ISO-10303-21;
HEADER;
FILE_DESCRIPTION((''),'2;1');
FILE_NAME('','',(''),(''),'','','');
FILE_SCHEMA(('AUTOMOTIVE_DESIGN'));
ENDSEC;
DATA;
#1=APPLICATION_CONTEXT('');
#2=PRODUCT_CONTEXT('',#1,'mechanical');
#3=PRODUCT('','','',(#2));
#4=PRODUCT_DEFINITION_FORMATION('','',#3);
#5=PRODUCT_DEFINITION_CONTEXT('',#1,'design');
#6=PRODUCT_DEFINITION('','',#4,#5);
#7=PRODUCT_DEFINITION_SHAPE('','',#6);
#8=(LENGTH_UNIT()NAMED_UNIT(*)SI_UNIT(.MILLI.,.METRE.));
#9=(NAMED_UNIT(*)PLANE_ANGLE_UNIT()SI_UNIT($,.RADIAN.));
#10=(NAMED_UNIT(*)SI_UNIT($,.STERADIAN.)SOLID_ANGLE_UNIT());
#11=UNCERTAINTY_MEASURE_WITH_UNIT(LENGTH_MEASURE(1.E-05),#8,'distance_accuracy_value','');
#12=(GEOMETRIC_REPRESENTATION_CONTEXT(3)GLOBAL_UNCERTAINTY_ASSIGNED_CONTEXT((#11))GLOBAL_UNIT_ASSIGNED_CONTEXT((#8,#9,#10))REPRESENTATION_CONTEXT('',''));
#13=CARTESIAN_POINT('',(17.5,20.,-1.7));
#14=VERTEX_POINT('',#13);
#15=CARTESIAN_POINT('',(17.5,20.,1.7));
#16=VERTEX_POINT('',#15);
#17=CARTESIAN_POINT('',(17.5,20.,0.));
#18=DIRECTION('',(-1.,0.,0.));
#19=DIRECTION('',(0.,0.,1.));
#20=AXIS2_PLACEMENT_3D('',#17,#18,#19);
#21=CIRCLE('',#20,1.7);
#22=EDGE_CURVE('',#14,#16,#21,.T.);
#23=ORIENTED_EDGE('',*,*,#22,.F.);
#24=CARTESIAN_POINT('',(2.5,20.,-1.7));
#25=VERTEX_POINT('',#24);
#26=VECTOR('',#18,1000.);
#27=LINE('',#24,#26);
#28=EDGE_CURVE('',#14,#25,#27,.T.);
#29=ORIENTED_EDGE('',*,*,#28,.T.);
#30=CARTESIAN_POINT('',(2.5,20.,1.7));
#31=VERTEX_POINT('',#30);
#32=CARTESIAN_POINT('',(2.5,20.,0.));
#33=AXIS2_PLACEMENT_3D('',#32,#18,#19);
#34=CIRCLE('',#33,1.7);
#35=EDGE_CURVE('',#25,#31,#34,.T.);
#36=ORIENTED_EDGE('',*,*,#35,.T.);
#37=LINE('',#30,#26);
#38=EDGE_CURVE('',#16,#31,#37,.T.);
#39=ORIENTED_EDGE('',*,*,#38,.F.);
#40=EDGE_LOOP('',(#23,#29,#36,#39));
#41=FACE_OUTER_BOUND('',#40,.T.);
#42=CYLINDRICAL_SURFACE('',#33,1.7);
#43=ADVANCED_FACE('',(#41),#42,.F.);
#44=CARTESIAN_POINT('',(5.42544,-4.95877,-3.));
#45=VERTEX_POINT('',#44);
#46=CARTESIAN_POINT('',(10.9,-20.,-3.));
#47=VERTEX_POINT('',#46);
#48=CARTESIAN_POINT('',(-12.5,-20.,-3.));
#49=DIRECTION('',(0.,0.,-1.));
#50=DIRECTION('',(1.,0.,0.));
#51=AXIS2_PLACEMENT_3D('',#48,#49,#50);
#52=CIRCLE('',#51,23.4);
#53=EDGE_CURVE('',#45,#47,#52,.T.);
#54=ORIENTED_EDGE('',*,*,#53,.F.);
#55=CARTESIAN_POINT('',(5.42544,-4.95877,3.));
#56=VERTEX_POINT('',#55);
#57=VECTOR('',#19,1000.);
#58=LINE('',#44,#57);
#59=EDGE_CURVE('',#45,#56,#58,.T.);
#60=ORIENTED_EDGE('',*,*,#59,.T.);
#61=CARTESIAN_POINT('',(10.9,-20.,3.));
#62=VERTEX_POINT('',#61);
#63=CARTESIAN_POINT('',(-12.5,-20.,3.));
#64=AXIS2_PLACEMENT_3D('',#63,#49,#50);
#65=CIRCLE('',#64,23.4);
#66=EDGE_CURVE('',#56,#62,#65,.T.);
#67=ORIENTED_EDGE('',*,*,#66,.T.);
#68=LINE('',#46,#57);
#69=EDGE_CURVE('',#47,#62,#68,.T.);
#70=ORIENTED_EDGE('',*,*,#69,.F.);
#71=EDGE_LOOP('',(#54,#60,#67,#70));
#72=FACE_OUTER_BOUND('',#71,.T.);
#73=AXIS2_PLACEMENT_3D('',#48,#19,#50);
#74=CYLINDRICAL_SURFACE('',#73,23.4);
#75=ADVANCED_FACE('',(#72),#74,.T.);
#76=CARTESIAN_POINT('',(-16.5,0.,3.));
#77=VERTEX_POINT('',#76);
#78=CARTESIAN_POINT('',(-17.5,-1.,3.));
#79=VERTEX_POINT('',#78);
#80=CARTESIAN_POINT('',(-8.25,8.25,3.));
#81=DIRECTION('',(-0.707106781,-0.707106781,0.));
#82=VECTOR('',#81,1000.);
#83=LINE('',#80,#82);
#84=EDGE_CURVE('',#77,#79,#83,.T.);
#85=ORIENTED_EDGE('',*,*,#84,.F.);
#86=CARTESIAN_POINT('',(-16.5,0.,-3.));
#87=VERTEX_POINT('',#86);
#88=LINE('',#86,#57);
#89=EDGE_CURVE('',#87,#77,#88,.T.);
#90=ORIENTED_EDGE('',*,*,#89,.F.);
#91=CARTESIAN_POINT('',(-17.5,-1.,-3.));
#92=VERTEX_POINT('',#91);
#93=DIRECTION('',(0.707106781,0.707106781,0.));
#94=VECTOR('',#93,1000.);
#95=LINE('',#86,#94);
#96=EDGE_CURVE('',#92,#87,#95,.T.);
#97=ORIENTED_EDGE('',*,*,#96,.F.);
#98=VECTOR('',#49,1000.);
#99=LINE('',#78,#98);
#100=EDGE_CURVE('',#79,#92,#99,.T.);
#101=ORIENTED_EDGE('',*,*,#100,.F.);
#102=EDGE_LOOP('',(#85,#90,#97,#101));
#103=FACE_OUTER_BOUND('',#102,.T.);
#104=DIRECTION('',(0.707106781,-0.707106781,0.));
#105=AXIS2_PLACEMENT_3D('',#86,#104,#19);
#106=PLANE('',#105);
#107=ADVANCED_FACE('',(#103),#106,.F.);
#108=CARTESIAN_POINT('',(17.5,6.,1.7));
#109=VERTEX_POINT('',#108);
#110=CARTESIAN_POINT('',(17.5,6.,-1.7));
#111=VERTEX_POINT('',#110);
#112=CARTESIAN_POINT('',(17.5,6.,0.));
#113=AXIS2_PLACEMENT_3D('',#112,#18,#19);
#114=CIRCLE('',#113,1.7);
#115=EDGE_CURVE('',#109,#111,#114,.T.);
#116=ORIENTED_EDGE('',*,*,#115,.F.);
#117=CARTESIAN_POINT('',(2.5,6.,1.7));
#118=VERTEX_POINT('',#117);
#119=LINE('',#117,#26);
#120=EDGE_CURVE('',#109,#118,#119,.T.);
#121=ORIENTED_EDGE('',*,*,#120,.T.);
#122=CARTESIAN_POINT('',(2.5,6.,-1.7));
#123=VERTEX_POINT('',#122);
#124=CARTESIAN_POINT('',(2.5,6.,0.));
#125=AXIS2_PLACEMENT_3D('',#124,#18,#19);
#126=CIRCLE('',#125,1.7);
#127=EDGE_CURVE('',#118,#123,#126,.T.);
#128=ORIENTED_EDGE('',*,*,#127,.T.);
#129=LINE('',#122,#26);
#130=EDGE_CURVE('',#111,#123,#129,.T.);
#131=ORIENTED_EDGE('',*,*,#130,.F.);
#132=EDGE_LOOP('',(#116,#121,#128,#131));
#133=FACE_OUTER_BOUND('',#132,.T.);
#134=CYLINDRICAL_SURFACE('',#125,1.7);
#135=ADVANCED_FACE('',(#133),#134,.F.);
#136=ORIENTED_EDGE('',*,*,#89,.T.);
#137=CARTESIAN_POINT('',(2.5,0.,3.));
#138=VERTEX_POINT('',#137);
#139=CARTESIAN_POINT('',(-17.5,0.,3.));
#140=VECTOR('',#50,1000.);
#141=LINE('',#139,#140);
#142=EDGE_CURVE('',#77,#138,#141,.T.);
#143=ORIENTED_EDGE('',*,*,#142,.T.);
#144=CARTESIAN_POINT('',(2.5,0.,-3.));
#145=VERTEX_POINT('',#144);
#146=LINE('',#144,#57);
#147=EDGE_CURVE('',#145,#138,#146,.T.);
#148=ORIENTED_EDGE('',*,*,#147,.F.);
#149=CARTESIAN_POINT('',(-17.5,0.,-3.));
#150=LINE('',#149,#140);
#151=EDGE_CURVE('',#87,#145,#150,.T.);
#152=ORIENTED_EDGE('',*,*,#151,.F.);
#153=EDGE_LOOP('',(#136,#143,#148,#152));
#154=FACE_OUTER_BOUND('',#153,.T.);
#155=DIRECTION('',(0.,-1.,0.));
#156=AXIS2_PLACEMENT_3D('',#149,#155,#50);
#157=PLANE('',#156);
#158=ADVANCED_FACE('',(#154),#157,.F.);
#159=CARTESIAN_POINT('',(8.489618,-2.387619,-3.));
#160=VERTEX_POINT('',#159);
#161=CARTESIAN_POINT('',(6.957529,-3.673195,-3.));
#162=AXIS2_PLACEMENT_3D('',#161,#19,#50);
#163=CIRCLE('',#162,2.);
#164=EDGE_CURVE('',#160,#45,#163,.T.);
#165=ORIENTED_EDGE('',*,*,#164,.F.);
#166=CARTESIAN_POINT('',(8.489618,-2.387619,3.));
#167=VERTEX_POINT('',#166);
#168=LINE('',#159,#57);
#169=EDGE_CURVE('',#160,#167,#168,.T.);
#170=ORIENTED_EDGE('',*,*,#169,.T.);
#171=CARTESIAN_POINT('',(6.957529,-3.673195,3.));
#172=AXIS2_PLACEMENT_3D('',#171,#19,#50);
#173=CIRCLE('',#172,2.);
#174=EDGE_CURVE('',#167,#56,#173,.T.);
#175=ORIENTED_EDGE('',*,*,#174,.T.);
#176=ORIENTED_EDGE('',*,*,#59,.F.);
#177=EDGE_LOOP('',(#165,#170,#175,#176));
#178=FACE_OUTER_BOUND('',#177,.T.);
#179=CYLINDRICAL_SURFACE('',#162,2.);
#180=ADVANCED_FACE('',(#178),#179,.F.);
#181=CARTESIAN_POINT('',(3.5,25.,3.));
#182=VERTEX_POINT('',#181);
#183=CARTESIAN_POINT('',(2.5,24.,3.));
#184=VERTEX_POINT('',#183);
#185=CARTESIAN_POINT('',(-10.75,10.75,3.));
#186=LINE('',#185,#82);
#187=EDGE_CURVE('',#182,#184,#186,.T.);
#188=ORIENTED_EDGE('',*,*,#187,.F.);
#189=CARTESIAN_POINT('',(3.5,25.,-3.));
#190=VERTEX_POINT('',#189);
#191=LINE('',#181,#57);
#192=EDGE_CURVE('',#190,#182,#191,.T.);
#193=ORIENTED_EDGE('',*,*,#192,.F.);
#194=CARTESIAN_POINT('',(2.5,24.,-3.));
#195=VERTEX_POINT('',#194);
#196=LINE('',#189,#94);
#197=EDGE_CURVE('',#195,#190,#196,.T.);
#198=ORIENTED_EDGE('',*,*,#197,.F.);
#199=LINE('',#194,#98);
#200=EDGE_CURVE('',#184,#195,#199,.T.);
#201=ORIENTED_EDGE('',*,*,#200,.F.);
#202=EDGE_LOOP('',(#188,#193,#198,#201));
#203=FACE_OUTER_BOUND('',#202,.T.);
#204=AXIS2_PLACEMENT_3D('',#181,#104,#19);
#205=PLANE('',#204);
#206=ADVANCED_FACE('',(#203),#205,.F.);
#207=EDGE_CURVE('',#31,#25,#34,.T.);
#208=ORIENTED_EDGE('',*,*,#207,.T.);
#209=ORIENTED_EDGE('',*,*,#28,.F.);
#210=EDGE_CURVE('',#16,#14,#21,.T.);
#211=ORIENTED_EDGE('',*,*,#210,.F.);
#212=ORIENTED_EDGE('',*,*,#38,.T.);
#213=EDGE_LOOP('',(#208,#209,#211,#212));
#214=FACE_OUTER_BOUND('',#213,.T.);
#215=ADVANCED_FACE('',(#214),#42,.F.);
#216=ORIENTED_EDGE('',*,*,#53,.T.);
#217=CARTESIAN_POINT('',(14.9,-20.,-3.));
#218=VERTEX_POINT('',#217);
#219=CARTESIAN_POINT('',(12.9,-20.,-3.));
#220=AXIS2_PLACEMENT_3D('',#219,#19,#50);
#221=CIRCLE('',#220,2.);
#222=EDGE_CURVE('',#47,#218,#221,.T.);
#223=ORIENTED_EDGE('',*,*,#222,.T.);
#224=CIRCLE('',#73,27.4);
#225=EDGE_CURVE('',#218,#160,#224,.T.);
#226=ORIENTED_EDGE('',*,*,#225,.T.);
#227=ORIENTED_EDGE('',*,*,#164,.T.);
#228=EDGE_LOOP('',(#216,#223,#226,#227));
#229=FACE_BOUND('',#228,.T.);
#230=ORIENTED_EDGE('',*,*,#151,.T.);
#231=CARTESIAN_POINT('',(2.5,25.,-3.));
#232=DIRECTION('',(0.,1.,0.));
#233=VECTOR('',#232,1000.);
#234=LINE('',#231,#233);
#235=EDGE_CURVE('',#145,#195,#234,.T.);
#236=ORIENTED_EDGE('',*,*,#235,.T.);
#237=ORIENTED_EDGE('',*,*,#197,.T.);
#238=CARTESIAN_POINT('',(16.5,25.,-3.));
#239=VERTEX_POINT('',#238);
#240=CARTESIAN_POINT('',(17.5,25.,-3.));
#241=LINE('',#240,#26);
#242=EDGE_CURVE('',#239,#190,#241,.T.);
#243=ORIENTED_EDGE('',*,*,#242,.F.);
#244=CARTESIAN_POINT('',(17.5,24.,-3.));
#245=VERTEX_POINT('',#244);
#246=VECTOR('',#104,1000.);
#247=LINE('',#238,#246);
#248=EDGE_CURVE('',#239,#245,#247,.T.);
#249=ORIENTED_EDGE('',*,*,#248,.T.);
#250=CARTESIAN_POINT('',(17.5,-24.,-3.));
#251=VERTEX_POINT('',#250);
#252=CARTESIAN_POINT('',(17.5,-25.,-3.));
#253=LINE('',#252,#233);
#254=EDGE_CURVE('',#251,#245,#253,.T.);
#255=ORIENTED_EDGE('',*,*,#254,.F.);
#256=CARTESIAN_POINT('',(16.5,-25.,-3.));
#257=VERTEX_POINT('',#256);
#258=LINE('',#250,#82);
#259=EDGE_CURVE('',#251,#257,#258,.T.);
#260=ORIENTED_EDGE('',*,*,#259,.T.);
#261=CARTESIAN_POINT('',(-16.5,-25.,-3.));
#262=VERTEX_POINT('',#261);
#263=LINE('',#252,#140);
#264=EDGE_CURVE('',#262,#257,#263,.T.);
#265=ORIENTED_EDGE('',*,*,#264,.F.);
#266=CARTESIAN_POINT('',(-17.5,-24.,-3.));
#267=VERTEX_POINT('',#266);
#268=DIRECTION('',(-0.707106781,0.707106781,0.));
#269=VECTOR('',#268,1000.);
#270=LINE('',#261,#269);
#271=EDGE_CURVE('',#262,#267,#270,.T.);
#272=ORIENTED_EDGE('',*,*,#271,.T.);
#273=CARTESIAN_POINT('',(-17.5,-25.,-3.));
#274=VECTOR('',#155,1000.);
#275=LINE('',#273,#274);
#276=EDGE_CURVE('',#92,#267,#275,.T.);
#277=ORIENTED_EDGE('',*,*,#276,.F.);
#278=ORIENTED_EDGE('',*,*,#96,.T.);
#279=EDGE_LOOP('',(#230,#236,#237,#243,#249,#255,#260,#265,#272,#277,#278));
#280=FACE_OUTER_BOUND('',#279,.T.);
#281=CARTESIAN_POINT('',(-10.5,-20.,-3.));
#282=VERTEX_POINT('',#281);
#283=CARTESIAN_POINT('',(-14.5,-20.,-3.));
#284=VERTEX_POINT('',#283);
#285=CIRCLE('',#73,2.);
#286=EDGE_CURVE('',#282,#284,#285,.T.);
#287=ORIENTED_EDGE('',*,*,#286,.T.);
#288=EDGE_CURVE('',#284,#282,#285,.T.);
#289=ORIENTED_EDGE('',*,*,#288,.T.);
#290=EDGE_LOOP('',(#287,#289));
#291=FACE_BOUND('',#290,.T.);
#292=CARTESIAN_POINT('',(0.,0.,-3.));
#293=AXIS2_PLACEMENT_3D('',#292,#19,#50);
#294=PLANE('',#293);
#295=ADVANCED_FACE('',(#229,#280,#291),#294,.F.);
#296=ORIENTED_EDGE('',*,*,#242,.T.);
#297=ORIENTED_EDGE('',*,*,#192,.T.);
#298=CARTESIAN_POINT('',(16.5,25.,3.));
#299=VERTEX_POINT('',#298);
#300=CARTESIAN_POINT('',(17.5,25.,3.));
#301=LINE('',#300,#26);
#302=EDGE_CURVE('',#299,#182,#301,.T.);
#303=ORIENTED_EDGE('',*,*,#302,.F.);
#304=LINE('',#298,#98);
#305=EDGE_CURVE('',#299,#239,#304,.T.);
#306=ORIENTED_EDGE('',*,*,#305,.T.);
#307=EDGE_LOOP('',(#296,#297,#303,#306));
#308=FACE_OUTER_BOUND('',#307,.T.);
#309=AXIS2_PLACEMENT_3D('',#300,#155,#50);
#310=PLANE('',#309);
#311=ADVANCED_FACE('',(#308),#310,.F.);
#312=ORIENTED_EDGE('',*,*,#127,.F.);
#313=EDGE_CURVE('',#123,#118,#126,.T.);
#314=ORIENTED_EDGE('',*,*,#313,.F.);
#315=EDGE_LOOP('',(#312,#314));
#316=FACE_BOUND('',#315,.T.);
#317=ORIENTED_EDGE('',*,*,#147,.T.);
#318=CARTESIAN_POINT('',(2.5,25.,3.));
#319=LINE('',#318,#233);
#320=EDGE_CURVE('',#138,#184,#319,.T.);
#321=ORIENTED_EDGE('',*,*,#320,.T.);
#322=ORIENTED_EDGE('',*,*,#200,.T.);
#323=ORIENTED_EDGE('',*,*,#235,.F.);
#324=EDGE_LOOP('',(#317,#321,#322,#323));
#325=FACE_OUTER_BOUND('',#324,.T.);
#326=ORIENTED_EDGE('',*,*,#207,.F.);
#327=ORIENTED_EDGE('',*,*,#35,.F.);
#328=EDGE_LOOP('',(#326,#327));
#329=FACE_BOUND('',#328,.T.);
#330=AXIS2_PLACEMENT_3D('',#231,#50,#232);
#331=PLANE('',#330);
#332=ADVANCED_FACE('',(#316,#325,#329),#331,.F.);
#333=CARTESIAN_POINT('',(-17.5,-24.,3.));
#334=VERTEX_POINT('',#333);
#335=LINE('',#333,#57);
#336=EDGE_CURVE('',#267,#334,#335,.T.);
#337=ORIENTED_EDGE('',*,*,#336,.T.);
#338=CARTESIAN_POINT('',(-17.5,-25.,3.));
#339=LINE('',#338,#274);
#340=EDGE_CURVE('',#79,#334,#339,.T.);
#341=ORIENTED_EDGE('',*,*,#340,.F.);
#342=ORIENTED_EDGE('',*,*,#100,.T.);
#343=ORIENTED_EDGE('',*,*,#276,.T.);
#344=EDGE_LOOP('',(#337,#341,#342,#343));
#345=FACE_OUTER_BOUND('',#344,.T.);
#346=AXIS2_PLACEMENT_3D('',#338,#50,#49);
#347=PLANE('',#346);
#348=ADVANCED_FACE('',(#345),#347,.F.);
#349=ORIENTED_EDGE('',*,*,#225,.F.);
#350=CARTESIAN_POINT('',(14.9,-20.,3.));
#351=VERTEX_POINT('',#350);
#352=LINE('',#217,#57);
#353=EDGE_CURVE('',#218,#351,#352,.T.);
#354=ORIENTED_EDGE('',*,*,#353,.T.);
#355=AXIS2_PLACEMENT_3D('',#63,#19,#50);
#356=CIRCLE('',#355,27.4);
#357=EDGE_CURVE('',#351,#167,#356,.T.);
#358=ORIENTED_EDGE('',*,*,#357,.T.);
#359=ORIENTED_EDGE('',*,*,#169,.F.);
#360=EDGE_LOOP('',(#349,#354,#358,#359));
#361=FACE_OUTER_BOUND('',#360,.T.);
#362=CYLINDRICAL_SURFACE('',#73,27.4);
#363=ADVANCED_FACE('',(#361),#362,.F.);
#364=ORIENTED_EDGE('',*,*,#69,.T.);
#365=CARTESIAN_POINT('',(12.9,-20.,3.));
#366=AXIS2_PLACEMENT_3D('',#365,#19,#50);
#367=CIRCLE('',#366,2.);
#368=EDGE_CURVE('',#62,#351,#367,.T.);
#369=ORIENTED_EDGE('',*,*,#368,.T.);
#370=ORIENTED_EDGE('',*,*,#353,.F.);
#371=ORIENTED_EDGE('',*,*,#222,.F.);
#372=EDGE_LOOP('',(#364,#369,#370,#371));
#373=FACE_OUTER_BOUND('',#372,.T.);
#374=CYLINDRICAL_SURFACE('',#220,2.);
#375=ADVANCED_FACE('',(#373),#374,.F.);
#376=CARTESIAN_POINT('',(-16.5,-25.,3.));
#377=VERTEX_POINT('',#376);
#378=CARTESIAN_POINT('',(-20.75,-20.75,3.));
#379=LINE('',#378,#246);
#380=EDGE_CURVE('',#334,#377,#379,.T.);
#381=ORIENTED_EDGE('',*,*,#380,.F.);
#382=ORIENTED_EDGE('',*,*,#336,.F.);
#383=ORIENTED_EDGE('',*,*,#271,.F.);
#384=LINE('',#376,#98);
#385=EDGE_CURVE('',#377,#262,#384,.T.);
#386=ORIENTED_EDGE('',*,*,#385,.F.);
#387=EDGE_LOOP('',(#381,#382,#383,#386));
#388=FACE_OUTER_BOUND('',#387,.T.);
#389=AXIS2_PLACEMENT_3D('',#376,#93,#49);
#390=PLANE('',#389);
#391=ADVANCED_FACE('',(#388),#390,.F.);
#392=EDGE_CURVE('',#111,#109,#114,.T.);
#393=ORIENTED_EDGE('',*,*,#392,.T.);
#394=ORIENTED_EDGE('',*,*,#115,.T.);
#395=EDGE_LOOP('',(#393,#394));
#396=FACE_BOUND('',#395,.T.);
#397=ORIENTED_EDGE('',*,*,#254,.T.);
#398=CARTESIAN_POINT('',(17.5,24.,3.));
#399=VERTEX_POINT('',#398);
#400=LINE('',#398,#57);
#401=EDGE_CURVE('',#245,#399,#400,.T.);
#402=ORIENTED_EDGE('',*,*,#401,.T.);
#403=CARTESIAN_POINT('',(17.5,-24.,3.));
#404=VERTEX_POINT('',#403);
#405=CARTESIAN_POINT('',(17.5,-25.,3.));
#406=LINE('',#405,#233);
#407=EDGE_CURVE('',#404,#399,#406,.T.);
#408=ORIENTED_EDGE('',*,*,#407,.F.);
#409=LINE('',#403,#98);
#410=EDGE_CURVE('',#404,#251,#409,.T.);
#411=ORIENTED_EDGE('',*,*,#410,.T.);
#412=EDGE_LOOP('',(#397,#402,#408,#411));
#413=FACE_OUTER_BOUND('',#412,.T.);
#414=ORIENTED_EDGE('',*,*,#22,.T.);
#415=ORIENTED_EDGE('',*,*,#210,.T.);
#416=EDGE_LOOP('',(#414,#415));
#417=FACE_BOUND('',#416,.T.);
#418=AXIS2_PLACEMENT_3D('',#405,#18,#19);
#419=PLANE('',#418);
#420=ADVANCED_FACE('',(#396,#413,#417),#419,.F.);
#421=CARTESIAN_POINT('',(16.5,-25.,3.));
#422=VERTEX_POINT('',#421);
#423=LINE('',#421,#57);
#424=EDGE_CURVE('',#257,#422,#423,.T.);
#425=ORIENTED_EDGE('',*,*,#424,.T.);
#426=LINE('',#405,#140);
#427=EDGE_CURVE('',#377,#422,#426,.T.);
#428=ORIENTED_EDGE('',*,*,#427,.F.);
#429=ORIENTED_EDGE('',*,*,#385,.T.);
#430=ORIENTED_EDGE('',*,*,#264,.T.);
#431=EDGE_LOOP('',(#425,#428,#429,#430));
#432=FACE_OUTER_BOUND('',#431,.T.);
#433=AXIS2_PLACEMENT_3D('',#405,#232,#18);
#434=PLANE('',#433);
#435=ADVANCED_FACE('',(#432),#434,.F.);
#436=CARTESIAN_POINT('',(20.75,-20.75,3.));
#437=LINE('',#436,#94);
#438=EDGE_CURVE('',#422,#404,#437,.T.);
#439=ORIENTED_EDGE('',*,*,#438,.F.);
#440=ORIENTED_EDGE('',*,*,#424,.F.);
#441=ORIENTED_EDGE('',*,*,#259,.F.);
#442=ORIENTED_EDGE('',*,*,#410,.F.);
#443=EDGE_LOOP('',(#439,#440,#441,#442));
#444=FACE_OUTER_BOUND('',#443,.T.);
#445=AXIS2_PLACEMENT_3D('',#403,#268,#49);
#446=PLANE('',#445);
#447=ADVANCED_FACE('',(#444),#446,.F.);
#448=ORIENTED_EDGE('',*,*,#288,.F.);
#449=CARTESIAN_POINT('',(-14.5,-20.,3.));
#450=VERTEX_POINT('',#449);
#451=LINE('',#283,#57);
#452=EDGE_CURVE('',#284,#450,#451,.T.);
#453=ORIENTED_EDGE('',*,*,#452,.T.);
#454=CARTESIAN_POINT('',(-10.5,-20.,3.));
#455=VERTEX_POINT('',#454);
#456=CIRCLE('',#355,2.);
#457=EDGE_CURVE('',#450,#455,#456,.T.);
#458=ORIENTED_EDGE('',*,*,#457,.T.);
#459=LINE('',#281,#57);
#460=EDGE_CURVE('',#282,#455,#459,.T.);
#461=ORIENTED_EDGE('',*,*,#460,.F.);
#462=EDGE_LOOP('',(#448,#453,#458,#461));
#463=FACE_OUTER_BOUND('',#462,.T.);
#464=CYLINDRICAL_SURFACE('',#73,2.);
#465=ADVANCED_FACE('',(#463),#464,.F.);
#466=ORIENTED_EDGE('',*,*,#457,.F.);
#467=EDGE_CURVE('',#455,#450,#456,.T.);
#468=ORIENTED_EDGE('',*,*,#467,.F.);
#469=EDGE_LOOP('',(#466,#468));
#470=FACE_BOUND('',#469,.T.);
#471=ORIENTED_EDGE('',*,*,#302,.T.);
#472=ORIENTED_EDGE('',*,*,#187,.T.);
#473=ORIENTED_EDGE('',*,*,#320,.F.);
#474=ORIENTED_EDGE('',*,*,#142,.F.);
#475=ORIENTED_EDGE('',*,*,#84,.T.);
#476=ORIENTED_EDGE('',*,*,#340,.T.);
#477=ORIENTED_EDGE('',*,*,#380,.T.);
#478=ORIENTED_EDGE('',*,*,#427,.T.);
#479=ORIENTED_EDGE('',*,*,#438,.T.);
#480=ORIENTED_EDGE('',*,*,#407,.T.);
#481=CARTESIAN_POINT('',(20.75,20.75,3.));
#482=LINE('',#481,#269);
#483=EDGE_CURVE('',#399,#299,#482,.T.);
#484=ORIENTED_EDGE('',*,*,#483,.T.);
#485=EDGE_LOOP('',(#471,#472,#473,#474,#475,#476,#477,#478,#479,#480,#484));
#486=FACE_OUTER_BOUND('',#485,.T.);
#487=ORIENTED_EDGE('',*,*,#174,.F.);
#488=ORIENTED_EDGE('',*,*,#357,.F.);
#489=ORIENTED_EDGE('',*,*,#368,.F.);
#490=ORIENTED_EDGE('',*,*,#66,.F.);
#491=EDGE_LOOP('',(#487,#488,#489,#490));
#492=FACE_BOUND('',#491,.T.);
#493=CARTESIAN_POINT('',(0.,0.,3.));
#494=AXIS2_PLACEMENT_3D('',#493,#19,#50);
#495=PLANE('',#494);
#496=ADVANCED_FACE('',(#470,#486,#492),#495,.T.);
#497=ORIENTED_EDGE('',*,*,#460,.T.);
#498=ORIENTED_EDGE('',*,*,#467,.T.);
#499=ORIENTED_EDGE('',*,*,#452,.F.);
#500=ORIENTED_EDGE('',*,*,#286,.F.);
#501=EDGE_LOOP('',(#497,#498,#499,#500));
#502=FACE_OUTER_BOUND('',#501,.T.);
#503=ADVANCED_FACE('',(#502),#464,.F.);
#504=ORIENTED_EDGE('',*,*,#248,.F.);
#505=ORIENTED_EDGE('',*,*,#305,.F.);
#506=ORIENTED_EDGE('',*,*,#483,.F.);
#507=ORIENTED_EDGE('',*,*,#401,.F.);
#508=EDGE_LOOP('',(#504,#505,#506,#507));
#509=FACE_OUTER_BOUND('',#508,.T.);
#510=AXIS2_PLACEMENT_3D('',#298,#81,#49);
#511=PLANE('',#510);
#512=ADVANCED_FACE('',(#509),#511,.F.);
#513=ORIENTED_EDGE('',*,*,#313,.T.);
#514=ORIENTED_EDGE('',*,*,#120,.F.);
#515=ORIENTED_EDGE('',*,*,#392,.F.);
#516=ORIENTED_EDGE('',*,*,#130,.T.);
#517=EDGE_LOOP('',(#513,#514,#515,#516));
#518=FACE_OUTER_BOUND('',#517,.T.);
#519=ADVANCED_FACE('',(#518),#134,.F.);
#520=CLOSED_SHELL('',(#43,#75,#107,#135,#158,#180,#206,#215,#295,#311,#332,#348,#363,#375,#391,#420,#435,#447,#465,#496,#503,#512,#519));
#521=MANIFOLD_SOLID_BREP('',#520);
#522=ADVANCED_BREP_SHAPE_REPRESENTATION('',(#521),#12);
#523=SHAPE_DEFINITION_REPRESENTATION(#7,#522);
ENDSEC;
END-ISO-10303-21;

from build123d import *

# Parameters (mm, degrees)
SKETCH_1_W          = 35
SKETCH_1_H          = 50
EXTRUDE_1_DEPTH     = 3
SKETCH_2_W          = 20
SKETCH_2_H          = 25
CUT_EXTRUDE_1_DEPTH = 32.10064308
SKETCH_3_R          = 2
CUT_EXTRUDE_2_DEPTH = 32.10064308
HOLE_WIZARD_M3_1_D  = 3.4
CHAMFER_1_SIZE      = 1


with BuildPart() as part:
    # 草图1 → 凸台-拉伸1 (new, symmetric)
    with BuildSketch(Plane.XY):
        Rectangle(SKETCH_1_W, SKETCH_1_H)
    extrude(amount=EXTRUDE_1_DEPTH, both=True)

    # 草图2 → 切除-拉伸1 (cut, through all)
    with BuildSketch(Plane.XY.offset(3)):
        with Locations((-7.5, 12.5)):
            Rectangle(SKETCH_2_W, SKETCH_2_H)
    extrude(amount=-CUT_EXTRUDE_1_DEPTH, mode=Mode.SUBTRACT)

    # 草图3 → 切除-拉伸2 (cut, through all)
    with BuildSketch(Plane.XY.offset(3)):
        with Locations((-12.5, -20)):
            Circle(SKETCH_3_R)
        with BuildLine():
            ThreePointArc((14.9, -20), (13.24757781, -10.628648073), (8.489617741, -2.387619495))
            ThreePointArc((8.489617741, -2.387619495), (5.671953636, -2.141105828), (5.425439969, -4.958769933))
            ThreePointArc((5.425439969, -4.958769933), (9.488807326, -11.996728646), (10.9, -20))
            ThreePointArc((10.9, -20), (12.9, -22), (14.9, -20))
        make_face()
    extrude(amount=-CUT_EXTRUDE_2_DEPTH, mode=Mode.SUBTRACT)

    # M3 间隙孔1 (through all)
    with Locations(Plane.ZY.offset(-2.5)):
        with Locations((0, 20), (0, 6)):
            Hole(HOLE_WIZARD_M3_1_D / 2)

    # 倒角1
    chamfer_1_edges = [part.edges().sort_by_distance(p)[0] for p in [
        (-17.5, 0, 0),
        (2.5, 25, 0),
        (17.5, 25, 0),
        (17.5, -25, 0),
        (-17.5, -25, 0),
    ]]
    chamfer(chamfer_1_edges, length=CHAMFER_1_SIZE)


solid = part.part
